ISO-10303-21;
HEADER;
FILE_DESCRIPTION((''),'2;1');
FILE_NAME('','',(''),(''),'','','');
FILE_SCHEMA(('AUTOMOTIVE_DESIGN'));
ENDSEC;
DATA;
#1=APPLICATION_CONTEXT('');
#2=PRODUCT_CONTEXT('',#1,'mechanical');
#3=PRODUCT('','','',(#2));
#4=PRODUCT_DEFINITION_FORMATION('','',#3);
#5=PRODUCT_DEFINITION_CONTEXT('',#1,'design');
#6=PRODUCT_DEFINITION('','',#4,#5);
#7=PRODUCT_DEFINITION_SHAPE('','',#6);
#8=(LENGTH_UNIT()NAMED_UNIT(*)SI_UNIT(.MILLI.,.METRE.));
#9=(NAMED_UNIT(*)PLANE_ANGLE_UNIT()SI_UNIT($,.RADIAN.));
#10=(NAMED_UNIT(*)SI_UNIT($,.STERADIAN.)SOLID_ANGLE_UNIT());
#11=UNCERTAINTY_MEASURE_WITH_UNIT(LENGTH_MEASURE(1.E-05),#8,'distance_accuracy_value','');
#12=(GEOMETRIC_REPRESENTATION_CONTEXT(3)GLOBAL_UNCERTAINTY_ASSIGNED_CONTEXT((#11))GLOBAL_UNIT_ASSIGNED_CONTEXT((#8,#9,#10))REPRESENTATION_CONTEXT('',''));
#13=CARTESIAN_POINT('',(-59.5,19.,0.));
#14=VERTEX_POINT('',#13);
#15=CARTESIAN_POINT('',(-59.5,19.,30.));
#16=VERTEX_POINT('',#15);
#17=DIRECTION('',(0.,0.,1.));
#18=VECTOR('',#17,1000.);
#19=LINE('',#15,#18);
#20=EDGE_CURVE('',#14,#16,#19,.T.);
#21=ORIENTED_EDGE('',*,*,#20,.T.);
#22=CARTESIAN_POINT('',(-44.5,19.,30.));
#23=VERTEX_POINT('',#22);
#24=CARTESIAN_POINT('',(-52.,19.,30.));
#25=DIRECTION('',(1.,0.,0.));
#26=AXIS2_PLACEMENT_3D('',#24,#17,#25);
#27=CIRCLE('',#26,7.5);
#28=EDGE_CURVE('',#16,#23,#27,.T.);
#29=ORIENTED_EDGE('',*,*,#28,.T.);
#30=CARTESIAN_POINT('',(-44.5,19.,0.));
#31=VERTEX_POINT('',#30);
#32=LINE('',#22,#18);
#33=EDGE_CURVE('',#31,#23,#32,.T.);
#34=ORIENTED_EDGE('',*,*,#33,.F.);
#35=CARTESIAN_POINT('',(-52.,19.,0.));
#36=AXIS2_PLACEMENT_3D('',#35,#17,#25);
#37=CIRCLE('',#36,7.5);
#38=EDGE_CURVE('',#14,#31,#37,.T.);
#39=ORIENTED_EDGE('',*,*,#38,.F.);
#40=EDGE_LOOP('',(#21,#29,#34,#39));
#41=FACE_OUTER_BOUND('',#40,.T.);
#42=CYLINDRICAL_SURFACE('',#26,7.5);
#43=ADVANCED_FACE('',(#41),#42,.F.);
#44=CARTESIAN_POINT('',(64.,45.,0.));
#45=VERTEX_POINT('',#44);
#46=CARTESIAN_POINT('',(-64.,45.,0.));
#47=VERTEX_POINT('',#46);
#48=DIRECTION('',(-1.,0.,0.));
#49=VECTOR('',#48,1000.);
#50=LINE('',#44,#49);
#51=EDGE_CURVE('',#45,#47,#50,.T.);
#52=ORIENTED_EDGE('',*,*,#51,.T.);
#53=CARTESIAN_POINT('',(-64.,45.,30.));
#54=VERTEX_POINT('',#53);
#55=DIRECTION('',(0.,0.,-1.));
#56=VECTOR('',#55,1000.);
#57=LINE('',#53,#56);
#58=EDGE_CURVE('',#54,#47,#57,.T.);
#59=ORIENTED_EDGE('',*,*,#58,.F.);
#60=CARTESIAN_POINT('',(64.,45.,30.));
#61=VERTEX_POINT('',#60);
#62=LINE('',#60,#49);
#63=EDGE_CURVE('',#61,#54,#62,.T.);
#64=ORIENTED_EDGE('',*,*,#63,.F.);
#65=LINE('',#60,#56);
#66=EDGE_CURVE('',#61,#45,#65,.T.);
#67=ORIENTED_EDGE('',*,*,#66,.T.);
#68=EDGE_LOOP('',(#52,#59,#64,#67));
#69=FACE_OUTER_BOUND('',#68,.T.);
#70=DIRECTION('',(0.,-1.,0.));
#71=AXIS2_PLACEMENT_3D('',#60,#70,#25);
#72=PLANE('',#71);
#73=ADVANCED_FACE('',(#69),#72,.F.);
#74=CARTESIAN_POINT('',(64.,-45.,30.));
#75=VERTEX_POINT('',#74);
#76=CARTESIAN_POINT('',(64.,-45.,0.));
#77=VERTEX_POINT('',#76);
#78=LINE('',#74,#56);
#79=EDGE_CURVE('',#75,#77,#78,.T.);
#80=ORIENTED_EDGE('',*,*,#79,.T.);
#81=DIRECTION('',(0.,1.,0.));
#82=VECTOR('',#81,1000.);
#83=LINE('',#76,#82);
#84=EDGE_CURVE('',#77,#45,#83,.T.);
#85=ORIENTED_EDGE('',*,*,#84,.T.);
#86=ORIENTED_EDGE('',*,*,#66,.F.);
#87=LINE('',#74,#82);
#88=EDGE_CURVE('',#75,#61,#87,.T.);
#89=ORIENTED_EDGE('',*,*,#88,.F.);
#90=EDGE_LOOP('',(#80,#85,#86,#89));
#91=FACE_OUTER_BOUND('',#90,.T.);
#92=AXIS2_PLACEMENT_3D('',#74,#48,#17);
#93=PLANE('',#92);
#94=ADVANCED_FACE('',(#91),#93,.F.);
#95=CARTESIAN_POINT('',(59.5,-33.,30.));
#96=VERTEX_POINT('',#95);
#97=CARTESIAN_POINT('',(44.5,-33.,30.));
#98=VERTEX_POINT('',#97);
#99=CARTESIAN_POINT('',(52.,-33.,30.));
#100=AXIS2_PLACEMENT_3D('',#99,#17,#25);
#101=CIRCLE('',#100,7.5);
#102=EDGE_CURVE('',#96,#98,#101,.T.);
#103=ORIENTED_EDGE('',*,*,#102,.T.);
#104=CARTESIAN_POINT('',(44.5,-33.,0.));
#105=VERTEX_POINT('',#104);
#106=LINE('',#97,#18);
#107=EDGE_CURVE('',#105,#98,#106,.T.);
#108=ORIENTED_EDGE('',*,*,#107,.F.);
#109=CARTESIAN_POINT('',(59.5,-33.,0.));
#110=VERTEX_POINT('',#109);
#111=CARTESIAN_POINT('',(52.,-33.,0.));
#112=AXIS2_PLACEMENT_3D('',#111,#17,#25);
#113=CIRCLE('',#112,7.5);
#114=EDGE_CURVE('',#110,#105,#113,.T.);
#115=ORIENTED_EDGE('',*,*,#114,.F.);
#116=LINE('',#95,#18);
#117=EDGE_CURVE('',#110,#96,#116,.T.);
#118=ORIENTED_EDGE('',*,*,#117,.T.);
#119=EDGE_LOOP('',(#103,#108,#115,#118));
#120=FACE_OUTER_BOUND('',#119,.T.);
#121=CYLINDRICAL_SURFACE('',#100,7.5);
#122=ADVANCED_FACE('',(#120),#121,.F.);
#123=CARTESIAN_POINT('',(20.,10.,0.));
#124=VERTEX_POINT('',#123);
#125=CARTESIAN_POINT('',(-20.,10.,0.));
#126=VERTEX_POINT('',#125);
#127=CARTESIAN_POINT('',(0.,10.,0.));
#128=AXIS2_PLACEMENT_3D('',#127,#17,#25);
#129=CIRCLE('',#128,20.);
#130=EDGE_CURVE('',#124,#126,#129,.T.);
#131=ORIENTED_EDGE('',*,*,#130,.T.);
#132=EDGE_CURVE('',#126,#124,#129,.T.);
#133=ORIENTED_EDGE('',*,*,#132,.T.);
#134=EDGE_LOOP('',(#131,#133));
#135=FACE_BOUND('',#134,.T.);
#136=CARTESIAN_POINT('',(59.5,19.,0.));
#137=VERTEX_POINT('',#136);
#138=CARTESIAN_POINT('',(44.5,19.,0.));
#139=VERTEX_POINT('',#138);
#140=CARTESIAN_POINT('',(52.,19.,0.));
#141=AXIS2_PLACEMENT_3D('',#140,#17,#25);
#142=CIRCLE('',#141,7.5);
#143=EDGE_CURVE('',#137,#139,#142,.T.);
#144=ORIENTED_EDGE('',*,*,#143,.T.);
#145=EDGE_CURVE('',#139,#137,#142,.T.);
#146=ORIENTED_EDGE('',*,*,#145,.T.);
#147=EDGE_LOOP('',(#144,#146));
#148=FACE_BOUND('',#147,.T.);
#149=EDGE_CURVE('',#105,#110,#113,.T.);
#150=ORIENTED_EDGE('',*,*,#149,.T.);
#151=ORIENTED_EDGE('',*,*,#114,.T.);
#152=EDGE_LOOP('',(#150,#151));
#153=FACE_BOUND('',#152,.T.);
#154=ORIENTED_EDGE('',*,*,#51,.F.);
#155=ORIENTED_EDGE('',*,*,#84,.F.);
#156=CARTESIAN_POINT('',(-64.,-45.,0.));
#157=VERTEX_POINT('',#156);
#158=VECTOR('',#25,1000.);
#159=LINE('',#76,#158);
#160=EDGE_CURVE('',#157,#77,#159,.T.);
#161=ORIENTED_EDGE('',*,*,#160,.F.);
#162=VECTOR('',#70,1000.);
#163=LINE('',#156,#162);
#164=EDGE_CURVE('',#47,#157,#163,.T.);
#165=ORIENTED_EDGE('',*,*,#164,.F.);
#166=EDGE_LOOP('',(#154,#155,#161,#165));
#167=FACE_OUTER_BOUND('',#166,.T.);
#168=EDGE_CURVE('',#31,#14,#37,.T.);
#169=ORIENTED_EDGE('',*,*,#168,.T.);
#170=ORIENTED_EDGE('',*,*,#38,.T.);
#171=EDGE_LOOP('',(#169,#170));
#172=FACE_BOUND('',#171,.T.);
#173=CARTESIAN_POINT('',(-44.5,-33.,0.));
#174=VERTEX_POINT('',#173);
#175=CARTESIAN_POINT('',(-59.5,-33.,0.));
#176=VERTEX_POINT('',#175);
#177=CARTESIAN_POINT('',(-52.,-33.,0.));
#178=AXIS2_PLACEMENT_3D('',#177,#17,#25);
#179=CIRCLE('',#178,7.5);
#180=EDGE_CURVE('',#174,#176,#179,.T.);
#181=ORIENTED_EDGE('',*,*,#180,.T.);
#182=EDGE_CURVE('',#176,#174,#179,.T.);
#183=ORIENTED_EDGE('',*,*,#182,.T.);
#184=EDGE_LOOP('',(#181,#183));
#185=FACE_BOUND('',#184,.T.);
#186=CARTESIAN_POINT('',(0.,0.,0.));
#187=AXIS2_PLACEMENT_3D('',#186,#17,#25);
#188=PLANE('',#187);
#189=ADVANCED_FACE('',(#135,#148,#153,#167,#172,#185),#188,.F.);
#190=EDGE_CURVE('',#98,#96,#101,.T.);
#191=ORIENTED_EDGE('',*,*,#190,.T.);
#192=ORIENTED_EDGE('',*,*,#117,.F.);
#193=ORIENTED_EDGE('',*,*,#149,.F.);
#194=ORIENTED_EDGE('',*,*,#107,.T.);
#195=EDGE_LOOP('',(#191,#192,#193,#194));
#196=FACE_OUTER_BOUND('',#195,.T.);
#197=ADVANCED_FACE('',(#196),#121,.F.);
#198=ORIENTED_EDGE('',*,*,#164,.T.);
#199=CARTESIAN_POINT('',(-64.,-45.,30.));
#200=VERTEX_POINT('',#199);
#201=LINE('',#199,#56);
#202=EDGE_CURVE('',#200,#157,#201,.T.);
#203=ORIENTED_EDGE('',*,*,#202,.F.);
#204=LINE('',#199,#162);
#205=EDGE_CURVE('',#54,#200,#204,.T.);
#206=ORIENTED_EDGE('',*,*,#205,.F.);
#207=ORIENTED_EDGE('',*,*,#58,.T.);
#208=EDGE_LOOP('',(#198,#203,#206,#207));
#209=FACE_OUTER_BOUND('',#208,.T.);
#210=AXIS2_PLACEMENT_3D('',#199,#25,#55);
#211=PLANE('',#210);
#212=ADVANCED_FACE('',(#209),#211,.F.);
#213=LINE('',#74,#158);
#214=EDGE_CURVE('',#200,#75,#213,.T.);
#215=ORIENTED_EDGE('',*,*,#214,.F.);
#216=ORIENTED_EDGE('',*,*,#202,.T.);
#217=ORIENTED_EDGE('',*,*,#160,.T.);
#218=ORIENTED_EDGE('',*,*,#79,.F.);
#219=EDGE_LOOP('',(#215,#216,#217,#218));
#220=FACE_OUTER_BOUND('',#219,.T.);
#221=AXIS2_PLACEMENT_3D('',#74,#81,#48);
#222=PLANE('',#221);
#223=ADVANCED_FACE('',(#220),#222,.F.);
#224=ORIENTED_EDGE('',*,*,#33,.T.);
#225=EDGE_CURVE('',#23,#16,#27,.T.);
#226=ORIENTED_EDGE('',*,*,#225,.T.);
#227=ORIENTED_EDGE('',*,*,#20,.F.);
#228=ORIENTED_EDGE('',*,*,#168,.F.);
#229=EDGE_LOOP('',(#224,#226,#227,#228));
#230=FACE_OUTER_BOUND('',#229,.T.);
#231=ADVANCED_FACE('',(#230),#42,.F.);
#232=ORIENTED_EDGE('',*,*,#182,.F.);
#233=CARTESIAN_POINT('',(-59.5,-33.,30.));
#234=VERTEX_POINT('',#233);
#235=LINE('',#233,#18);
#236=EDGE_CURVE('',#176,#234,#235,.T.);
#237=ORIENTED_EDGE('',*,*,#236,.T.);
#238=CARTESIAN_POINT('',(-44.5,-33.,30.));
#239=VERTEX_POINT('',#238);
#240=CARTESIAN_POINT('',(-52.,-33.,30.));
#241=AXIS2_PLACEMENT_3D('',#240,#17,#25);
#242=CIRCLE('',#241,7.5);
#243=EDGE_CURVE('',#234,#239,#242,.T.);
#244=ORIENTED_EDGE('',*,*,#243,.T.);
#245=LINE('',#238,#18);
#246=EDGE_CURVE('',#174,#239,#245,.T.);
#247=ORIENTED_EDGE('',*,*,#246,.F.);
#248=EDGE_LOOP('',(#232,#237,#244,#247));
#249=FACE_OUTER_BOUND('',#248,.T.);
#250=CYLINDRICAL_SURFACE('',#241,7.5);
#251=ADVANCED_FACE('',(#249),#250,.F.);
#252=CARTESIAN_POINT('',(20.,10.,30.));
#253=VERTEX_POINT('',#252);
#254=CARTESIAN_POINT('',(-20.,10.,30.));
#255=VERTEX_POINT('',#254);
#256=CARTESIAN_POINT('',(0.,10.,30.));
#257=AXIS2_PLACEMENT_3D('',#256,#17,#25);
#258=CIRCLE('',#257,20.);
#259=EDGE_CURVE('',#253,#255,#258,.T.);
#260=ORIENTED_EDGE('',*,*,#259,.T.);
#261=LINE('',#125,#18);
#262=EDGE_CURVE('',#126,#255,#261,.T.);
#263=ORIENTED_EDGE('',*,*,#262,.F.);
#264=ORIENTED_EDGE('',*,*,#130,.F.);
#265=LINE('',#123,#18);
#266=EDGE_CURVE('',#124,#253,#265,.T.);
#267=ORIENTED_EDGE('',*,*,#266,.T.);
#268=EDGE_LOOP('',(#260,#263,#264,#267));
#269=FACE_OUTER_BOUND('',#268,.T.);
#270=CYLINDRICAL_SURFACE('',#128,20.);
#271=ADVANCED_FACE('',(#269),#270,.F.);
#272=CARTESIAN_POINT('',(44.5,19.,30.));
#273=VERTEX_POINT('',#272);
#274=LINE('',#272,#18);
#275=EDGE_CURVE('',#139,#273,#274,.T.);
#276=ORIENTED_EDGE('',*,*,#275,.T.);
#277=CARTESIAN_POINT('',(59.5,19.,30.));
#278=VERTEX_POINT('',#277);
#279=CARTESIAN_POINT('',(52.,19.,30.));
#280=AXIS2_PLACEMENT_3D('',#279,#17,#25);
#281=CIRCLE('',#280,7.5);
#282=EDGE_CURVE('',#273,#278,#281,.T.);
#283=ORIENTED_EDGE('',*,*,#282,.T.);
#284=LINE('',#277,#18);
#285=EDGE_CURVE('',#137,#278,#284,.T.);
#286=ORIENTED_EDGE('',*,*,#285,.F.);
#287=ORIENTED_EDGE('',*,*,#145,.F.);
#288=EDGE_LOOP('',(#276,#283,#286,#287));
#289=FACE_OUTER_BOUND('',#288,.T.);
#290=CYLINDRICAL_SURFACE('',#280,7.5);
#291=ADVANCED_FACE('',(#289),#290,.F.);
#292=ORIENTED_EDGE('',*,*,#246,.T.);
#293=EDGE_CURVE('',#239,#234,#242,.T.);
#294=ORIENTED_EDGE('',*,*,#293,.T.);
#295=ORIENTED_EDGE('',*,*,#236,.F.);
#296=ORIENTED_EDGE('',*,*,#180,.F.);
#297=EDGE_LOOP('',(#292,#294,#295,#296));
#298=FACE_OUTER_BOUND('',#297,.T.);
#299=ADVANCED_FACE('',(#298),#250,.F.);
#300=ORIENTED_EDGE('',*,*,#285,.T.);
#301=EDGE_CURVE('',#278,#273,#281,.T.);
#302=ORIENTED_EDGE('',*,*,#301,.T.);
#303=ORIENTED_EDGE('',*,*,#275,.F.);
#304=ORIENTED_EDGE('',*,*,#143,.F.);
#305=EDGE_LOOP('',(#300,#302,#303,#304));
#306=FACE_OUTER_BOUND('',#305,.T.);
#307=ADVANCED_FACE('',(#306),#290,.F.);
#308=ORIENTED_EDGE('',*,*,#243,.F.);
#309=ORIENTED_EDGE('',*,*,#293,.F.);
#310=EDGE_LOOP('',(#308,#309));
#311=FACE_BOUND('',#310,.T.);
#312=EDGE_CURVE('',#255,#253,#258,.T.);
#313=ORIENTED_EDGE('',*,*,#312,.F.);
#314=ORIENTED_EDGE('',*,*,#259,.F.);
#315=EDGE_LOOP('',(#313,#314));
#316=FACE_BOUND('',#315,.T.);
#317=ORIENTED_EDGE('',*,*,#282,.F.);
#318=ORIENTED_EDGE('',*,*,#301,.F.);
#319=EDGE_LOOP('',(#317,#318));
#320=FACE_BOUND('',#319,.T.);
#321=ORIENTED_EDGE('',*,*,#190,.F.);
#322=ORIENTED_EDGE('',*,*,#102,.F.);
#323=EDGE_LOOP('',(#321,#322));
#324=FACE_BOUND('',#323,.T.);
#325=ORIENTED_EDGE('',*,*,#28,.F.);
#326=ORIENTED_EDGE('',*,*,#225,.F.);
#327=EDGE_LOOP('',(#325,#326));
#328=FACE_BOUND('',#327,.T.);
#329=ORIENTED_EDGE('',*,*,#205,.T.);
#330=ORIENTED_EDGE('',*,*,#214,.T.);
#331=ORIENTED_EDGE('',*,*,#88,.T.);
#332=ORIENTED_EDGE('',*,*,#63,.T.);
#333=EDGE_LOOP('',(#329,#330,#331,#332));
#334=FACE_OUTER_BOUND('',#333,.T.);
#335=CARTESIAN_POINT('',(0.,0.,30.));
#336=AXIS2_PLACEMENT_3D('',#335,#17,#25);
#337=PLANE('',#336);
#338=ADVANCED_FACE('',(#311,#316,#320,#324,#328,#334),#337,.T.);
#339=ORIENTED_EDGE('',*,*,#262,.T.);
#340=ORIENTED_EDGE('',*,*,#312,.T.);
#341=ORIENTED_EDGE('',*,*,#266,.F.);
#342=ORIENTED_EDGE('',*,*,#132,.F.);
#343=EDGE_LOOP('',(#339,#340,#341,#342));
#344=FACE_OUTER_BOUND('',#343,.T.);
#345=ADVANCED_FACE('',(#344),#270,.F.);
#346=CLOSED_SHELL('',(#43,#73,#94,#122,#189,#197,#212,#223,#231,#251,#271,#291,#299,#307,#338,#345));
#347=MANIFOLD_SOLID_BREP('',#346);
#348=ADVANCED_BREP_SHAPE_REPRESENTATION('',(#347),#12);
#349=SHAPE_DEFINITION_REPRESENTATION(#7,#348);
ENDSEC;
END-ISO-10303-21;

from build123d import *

# Parameters (mm, degrees)
SKETCH1_W                      = 128
SKETCH1_H                      = 90
BOSS_EXTRUDE1_DEPTH            = 30
SKETCH4_R                      = 20
CUT_EXTRUDE3_DEPTH             = 84.791407674
F_15_0_15_DIAMETER_HOLE1_D     = 15
F_15_0_15_DIAMETER_HOLE1_DEPTH = 42
F_15_0_15_DIAMETER_HOLE1_TIP   = 4.506454643


with BuildPart() as part:
    # Sketch1 → Boss-Extrude1 (new body)
    with BuildSketch(Plane.XY):
        Rectangle(SKETCH1_W, SKETCH1_H)
    extrude(amount=BOSS_EXTRUDE1_DEPTH)

    # Sketch4 → Cut-Extrude3 (cut, through all)
    with BuildSketch(Plane.XY.offset(30)):
        with Locations((0, 10)):
            Circle(SKETCH4_R)
    extrude(amount=-CUT_EXTRUDE3_DEPTH, mode=Mode.SUBTRACT)

    # Ø15.0 (15) Diameter Hole1
    with Locations(Plane.XY.offset(30)):
        with Locations((-52, 19), (-52, -33), (52, -33), (52, 19)):
            Hole(F_15_0_15_DIAMETER_HOLE1_D / 2, depth=F_15_0_15_DIAMETER_HOLE1_DEPTH)
            with Locations((0, 0, -(F_15_0_15_DIAMETER_HOLE1_DEPTH + F_15_0_15_DIAMETER_HOLE1_TIP / 2))):  # 118° drill point
                Cone(0, F_15_0_15_DIAMETER_HOLE1_D / 2, F_15_0_15_DIAMETER_HOLE1_TIP, mode=Mode.SUBTRACT)


solid = part.part
